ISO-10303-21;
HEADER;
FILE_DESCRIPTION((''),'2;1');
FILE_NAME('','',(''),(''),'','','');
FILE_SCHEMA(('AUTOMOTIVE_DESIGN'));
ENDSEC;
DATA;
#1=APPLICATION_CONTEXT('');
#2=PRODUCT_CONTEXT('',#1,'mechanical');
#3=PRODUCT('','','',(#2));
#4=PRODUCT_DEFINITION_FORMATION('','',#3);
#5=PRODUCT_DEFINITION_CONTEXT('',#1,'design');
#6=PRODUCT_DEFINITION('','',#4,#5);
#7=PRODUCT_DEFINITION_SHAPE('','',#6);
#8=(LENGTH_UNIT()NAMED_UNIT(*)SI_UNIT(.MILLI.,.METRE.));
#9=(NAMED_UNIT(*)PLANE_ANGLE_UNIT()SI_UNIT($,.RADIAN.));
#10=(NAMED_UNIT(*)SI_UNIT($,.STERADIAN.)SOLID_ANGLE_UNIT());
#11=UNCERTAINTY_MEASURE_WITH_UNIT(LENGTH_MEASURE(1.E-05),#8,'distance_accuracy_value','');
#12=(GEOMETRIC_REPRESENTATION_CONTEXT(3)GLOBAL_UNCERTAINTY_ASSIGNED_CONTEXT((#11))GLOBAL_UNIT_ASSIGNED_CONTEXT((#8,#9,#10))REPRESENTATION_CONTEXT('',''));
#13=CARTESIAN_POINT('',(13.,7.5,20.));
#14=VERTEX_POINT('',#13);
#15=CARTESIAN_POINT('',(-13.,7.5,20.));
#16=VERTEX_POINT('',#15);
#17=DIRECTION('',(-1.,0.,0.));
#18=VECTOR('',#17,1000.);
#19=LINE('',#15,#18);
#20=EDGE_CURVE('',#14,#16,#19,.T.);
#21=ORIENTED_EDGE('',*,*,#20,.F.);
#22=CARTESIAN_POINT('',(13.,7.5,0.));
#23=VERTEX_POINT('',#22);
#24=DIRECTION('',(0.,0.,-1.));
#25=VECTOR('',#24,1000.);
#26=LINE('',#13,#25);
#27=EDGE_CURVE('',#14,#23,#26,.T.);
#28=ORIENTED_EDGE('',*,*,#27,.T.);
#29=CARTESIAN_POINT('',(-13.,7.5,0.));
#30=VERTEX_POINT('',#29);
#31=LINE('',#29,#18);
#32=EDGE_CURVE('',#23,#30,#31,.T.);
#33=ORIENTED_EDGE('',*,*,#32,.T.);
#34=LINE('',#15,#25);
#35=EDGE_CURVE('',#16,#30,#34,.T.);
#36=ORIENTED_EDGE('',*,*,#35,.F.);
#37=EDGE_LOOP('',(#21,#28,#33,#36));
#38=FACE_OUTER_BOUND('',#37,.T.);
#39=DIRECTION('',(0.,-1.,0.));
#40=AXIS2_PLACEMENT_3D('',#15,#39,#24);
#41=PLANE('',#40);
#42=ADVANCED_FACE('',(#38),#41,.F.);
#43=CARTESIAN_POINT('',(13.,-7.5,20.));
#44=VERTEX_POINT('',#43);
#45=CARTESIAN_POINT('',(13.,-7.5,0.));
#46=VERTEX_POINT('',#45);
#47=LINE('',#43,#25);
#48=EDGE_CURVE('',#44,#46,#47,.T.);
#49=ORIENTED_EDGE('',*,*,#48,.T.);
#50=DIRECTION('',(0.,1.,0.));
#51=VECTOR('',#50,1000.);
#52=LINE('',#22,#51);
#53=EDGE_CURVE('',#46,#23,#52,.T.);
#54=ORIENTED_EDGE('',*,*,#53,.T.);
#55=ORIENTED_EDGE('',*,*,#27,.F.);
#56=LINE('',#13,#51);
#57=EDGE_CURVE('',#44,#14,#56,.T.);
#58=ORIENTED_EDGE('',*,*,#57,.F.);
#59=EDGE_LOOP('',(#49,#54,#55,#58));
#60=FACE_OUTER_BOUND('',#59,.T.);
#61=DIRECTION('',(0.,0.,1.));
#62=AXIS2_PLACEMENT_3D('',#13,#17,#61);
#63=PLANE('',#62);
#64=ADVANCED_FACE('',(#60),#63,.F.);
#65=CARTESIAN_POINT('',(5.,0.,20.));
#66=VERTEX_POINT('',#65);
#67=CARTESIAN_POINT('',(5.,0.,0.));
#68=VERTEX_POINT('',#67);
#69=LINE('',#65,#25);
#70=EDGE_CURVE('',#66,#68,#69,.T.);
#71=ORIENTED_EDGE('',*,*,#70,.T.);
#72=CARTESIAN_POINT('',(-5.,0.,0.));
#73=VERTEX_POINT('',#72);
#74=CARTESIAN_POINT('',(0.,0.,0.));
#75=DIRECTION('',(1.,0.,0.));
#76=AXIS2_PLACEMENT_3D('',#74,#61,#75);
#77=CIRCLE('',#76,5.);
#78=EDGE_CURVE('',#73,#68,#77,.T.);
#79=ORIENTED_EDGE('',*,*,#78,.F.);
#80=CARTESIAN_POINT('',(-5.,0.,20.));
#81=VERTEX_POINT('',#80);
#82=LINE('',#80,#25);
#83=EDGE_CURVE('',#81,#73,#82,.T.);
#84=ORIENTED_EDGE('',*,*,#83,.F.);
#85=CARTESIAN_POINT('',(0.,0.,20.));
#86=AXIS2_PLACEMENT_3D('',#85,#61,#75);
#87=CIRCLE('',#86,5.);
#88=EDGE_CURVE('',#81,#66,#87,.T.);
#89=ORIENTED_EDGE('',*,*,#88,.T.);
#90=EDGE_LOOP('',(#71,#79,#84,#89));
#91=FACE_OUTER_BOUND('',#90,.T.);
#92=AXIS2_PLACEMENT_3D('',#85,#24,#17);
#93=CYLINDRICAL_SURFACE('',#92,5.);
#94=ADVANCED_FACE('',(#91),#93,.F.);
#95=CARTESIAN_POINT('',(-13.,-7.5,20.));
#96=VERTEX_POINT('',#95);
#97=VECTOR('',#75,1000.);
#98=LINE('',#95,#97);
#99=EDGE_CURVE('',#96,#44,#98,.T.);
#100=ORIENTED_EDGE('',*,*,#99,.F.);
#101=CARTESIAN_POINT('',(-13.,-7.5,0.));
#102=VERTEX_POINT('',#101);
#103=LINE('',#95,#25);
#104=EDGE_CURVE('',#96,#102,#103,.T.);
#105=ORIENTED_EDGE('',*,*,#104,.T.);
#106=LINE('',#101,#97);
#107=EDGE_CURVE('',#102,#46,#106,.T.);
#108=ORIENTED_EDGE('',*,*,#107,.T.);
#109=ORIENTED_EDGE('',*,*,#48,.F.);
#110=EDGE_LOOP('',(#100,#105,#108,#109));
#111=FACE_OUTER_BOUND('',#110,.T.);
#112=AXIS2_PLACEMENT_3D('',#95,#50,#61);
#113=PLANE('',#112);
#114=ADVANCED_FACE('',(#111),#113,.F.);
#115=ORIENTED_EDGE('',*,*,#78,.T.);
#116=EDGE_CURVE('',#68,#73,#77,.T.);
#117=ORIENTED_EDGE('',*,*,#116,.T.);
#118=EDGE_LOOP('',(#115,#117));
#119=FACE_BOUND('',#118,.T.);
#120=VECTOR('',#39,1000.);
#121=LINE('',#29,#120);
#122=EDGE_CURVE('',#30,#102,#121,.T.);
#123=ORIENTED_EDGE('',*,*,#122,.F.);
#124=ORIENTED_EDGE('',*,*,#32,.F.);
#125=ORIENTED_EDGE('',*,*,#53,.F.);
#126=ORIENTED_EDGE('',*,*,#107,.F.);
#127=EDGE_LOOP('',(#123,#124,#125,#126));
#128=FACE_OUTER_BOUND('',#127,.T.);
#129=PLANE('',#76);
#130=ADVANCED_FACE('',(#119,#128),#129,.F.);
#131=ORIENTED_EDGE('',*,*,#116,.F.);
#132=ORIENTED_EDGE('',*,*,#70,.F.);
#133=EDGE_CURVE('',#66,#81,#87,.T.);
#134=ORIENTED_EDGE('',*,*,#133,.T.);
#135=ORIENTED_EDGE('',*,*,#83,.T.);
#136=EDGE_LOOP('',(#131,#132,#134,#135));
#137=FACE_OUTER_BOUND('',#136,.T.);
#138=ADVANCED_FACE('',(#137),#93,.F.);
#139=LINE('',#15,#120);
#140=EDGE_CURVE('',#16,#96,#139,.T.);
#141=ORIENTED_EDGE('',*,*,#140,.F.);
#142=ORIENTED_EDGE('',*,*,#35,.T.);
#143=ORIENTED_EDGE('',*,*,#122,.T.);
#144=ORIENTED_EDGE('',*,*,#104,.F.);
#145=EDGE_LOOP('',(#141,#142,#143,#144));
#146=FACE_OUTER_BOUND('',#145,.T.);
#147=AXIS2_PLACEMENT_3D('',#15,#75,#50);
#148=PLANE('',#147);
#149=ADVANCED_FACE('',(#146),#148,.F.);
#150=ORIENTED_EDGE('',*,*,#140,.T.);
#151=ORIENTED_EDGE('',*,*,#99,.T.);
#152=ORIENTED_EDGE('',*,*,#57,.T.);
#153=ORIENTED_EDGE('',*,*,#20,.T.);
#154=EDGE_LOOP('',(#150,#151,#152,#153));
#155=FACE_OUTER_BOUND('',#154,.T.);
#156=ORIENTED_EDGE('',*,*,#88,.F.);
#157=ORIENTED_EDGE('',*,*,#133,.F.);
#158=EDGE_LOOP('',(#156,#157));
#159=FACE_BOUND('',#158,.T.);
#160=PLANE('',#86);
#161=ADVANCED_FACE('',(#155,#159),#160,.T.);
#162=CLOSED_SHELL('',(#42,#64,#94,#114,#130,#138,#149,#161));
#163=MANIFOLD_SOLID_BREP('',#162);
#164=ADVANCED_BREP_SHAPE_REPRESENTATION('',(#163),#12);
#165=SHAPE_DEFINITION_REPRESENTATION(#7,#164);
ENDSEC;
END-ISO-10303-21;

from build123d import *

# Parameters (mm, degrees)
SKETCH1_W           = 26
SKETCH1_H           = 15
SKETCH1_R           = 5
BOSS_EXTRUDE1_DEPTH = 20


with BuildPart() as part:
    # Sketch1 → Boss-Extrude1 (new body)
    with BuildSketch(Plane.XY):
        Rectangle(SKETCH1_W, SKETCH1_H)
        Circle(SKETCH1_R, mode=Mode.SUBTRACT)
    extrude(amount=BOSS_EXTRUDE1_DEPTH)


solid = part.part
